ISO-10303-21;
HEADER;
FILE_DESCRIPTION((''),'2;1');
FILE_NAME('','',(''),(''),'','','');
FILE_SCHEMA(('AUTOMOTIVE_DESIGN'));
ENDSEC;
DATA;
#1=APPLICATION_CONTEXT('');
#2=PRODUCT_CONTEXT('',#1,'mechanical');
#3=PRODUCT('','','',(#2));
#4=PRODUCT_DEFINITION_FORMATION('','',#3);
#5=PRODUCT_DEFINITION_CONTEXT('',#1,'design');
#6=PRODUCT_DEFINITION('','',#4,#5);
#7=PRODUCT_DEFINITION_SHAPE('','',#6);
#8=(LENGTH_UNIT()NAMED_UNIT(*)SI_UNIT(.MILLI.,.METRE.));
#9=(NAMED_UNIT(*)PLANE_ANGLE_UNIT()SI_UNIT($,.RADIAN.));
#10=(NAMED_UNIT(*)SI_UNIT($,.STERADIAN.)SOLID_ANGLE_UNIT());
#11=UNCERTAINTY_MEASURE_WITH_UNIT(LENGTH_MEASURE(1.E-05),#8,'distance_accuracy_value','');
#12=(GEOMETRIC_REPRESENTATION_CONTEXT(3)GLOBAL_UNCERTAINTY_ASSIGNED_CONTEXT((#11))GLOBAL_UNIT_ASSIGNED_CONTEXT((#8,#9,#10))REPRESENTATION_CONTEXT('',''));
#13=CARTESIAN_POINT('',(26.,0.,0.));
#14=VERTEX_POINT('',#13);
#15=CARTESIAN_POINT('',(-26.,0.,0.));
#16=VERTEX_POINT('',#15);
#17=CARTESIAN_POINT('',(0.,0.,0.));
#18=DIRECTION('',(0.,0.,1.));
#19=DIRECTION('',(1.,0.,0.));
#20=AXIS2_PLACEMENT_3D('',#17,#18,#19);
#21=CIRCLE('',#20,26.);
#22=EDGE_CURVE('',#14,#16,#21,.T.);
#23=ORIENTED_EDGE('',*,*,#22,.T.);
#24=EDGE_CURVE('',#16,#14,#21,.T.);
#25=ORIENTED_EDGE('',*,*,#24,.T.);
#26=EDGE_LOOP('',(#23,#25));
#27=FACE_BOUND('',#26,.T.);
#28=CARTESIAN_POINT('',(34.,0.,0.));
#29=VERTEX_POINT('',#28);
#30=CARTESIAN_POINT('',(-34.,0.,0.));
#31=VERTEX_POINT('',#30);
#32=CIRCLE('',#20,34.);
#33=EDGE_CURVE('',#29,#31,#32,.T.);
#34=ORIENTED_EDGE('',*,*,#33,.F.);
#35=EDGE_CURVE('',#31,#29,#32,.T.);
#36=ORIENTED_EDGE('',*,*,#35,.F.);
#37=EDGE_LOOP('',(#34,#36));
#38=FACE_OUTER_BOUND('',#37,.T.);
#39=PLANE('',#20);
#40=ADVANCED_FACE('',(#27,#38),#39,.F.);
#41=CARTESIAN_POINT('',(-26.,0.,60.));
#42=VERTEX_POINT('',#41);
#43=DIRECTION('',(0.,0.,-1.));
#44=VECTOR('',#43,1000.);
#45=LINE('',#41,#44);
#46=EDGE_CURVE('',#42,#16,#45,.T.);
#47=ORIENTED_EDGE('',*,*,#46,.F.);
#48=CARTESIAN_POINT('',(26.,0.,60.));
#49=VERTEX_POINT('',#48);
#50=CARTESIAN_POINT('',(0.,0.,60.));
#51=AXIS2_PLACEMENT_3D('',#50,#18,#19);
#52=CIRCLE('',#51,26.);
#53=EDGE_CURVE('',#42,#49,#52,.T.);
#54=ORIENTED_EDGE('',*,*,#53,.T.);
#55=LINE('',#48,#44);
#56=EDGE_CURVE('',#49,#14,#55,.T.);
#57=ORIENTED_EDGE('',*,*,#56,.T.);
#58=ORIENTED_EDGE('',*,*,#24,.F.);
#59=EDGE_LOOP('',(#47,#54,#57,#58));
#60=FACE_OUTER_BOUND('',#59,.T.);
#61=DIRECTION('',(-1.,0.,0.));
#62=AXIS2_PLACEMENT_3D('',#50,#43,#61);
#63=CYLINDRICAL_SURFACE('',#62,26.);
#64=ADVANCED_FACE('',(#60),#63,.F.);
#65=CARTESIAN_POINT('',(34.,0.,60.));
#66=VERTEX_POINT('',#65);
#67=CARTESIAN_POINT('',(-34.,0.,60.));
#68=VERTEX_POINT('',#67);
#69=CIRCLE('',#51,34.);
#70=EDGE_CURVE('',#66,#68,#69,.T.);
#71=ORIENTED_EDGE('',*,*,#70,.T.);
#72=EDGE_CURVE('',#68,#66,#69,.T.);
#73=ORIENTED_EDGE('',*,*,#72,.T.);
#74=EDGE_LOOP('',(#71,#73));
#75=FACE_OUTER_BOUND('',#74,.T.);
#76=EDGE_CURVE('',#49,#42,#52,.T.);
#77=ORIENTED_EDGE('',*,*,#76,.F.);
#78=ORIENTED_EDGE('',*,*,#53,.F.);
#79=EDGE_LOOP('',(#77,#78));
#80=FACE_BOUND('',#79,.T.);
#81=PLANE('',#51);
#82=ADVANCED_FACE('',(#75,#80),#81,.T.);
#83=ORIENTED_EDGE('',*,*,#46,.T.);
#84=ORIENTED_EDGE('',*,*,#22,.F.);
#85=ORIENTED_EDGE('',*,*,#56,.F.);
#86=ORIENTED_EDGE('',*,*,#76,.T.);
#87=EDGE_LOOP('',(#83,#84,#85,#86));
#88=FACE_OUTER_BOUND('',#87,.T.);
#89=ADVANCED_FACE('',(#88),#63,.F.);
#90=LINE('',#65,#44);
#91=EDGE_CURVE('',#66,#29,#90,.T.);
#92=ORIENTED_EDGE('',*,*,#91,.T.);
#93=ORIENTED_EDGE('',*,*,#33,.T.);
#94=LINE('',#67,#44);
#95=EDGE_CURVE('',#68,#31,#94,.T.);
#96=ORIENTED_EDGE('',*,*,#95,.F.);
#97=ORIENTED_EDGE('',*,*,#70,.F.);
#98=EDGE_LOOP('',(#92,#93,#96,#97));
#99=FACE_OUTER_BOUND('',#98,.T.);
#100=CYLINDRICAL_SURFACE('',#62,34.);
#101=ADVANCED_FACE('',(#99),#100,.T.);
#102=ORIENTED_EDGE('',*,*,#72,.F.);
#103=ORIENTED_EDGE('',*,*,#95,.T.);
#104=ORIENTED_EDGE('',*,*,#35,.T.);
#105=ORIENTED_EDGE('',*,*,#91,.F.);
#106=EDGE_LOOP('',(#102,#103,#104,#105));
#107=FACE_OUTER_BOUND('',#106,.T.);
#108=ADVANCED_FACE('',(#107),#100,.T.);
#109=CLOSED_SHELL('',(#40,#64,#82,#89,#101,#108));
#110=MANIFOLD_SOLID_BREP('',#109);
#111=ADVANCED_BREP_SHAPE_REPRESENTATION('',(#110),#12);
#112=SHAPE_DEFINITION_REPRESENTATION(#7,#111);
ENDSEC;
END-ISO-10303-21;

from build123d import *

# Parameters (mm, degrees)
SKETCH_1_R      = 34
SKETCH_1_R_2    = 26
EXTRUDE_1_DEPTH = 60


with BuildPart() as part:
    # 草图1 → 凸台-拉伸1 (new body)
    with BuildSketch(Plane.XY):
        Circle(SKETCH_1_R)
        Circle(SKETCH_1_R_2, mode=Mode.SUBTRACT)
    extrude(amount=EXTRUDE_1_DEPTH)


solid = part.part
